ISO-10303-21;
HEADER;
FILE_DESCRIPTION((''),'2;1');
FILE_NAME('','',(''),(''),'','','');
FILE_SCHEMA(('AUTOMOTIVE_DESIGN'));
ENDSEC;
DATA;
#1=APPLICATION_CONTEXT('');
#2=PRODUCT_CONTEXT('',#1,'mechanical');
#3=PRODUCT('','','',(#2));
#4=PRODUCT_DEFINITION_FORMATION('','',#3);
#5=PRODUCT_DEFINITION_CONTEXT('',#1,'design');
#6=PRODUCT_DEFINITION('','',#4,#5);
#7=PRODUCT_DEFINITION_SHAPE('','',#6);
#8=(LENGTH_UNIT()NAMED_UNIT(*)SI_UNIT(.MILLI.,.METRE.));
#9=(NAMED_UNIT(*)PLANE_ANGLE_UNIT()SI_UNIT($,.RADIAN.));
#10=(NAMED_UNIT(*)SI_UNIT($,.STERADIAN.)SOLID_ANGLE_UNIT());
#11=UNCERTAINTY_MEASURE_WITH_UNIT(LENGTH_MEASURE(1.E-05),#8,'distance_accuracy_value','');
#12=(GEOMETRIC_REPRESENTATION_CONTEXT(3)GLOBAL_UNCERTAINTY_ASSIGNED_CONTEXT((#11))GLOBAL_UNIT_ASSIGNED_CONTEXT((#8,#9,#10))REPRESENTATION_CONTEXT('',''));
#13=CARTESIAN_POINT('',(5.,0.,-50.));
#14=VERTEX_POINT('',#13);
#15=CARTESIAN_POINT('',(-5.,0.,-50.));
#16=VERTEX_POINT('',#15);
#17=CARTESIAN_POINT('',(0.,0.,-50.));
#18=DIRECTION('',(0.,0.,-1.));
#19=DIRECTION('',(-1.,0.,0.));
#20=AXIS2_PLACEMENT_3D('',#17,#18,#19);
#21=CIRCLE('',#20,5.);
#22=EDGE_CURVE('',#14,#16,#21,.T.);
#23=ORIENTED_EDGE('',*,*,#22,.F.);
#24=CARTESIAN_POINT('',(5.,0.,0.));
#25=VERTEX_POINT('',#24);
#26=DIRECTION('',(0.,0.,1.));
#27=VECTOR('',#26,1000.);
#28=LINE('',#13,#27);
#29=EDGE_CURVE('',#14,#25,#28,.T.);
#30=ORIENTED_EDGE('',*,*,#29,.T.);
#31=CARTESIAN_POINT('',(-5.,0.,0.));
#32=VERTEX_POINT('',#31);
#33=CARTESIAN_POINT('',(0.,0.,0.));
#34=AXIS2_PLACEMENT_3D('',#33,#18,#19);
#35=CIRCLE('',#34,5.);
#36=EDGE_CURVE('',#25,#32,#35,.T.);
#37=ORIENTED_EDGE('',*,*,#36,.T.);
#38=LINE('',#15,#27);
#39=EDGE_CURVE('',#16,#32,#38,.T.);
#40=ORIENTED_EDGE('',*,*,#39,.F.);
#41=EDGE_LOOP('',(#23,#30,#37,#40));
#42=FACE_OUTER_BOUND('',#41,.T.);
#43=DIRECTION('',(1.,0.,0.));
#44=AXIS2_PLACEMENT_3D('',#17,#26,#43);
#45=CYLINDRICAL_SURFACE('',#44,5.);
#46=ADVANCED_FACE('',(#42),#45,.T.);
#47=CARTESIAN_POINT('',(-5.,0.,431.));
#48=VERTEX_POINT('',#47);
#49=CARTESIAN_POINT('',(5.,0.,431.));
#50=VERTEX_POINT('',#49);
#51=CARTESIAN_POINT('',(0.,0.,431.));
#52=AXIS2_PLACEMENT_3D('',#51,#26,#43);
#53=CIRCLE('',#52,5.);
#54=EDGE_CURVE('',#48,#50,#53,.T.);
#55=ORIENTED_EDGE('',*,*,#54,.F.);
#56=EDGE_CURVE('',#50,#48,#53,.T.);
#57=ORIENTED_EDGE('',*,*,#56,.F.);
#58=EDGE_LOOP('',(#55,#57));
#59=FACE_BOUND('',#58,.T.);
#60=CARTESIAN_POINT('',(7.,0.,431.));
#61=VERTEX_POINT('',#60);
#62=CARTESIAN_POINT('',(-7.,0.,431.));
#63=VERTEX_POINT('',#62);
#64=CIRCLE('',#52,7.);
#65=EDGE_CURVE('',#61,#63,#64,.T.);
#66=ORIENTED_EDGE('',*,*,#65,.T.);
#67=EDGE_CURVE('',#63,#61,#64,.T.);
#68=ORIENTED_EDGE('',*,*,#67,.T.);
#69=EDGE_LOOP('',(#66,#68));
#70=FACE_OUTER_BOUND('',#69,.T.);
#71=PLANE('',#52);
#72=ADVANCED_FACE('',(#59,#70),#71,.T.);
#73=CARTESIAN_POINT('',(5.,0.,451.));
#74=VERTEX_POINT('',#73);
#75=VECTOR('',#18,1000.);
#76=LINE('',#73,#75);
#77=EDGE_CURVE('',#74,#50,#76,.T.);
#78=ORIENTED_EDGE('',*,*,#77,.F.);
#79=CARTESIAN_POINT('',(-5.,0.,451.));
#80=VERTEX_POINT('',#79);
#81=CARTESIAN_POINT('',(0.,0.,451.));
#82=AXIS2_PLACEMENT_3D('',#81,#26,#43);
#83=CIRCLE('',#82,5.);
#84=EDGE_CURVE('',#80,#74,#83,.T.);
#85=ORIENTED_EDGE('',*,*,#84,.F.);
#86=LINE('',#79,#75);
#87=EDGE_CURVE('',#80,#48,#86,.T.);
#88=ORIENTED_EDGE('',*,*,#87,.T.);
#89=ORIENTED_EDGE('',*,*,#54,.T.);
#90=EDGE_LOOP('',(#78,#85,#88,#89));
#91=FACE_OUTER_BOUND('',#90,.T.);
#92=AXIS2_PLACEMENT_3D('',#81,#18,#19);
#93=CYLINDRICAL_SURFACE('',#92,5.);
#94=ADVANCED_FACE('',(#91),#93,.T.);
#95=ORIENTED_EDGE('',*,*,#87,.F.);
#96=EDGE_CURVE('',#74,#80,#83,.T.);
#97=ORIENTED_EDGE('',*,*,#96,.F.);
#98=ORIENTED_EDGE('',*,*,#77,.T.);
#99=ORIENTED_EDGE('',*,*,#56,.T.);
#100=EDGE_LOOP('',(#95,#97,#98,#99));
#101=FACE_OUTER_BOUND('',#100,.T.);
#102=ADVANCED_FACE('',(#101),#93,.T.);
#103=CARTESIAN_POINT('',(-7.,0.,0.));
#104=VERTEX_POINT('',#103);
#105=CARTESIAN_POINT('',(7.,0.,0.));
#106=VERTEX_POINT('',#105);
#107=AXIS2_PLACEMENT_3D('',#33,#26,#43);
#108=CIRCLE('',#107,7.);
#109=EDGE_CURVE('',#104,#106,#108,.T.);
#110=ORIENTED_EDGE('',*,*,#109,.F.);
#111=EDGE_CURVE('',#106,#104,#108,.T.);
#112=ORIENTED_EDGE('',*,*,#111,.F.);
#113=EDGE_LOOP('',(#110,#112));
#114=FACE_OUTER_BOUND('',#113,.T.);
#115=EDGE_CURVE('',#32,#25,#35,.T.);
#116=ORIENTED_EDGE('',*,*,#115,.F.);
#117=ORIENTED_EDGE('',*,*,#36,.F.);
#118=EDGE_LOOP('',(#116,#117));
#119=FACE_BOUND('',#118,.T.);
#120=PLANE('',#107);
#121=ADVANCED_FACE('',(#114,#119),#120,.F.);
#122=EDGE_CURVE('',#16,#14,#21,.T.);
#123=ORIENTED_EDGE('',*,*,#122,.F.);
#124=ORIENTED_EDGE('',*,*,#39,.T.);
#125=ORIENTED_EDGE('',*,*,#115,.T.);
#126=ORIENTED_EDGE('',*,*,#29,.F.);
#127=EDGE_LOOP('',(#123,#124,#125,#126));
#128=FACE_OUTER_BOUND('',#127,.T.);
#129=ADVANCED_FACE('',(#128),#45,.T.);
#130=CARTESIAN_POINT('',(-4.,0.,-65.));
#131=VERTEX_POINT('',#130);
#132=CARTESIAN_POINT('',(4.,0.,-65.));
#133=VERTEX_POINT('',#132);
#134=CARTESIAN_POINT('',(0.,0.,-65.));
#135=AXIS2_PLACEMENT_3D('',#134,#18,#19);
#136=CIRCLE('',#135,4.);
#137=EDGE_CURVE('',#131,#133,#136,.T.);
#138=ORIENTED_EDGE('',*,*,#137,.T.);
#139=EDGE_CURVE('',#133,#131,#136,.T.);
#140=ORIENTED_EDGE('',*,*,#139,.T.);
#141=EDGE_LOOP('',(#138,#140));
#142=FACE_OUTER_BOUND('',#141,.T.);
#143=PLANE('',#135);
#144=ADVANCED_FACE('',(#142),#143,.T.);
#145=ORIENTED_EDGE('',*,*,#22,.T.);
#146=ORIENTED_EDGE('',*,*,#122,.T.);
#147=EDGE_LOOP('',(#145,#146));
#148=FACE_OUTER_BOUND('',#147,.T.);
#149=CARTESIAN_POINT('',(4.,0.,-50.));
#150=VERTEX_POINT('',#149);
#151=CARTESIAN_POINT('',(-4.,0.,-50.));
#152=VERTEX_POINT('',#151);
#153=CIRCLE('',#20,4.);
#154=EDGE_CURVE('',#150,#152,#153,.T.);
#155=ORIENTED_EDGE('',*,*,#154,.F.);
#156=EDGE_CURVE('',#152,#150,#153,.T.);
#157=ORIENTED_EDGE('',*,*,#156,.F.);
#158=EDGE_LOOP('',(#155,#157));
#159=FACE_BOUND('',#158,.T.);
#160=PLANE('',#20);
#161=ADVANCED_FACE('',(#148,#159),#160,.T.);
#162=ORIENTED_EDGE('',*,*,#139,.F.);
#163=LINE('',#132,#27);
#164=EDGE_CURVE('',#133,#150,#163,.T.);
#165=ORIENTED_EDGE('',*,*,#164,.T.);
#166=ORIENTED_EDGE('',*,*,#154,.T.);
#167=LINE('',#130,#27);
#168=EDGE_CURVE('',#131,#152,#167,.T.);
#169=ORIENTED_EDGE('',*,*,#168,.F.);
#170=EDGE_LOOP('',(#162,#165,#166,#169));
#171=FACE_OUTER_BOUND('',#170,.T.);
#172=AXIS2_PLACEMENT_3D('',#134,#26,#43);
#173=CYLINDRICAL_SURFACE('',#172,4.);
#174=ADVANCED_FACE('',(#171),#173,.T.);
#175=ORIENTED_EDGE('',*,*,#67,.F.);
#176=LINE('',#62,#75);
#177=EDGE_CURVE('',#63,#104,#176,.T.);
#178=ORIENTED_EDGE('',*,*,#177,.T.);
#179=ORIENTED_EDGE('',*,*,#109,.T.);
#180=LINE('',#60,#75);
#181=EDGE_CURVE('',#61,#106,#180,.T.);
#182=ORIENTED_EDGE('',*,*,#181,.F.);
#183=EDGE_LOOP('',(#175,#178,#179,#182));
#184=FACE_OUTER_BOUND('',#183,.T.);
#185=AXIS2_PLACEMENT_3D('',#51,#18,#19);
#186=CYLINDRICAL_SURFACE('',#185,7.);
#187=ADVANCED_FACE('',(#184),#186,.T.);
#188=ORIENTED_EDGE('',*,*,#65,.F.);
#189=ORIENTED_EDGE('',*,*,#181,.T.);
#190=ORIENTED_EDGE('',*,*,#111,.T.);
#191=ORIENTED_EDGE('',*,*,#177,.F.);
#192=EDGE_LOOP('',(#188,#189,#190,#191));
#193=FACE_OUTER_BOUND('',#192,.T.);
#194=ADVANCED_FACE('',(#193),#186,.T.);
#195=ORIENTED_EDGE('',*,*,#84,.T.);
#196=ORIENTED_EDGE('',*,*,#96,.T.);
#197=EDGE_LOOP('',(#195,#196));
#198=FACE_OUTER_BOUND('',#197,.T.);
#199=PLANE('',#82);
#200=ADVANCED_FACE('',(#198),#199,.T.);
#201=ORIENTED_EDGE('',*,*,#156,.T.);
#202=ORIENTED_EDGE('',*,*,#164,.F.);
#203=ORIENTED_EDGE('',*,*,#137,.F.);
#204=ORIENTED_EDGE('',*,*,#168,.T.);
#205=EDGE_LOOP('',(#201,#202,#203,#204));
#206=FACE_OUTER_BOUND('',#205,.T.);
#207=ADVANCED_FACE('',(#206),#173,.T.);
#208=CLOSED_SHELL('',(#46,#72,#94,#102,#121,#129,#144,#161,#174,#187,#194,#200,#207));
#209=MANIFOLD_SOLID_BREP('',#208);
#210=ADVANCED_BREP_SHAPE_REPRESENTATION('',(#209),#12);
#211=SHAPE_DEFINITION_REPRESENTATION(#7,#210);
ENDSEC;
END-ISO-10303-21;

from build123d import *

# Parameters (mm, degrees)
SKETCH1_R           = 7
BOSS_EXTRUDE1_DEPTH = 431
SKETCH2_R           = 5
BOSS_EXTRUDE2_DEPTH = 20
BOSS_EXTRUDE3_START = 50
SKETCH3_R           = 5
BOSS_EXTRUDE3_DEPTH = 50
SKETCH4_R           = 4
BOSS_EXTRUDE4_DEPTH = 15


with BuildPart() as part:
    # Sketch1 → Boss-Extrude1 (new body)
    with BuildSketch(Plane.XY):
        Circle(SKETCH1_R)
    extrude(amount=BOSS_EXTRUDE1_DEPTH)

    # Sketch2 → Boss-Extrude2 (add)
    with BuildSketch(Plane.XY.offset(431)):
        Circle(SKETCH2_R)
    extrude(amount=BOSS_EXTRUDE2_DEPTH)

    # Sketch3 → Boss-Extrude3 (add)
    with BuildSketch(Plane(origin=(0, 0, 0), x_dir=(-1, 0, 0), z_dir=(0, 0, -1)).offset(BOSS_EXTRUDE3_START)):
        with Locations(Location((0, 0, 0), (0, 0, 180))):
            Circle(SKETCH3_R)
    extrude(amount=-BOSS_EXTRUDE3_DEPTH)

    # Sketch4 → Boss-Extrude4 (add)
    with BuildSketch(Plane(origin=(0, 0, -50), x_dir=(-1, 0, 0), z_dir=(0, 0, -1))):
        Circle(SKETCH4_R)
    extrude(amount=BOSS_EXTRUDE4_DEPTH)


solid = part.part
